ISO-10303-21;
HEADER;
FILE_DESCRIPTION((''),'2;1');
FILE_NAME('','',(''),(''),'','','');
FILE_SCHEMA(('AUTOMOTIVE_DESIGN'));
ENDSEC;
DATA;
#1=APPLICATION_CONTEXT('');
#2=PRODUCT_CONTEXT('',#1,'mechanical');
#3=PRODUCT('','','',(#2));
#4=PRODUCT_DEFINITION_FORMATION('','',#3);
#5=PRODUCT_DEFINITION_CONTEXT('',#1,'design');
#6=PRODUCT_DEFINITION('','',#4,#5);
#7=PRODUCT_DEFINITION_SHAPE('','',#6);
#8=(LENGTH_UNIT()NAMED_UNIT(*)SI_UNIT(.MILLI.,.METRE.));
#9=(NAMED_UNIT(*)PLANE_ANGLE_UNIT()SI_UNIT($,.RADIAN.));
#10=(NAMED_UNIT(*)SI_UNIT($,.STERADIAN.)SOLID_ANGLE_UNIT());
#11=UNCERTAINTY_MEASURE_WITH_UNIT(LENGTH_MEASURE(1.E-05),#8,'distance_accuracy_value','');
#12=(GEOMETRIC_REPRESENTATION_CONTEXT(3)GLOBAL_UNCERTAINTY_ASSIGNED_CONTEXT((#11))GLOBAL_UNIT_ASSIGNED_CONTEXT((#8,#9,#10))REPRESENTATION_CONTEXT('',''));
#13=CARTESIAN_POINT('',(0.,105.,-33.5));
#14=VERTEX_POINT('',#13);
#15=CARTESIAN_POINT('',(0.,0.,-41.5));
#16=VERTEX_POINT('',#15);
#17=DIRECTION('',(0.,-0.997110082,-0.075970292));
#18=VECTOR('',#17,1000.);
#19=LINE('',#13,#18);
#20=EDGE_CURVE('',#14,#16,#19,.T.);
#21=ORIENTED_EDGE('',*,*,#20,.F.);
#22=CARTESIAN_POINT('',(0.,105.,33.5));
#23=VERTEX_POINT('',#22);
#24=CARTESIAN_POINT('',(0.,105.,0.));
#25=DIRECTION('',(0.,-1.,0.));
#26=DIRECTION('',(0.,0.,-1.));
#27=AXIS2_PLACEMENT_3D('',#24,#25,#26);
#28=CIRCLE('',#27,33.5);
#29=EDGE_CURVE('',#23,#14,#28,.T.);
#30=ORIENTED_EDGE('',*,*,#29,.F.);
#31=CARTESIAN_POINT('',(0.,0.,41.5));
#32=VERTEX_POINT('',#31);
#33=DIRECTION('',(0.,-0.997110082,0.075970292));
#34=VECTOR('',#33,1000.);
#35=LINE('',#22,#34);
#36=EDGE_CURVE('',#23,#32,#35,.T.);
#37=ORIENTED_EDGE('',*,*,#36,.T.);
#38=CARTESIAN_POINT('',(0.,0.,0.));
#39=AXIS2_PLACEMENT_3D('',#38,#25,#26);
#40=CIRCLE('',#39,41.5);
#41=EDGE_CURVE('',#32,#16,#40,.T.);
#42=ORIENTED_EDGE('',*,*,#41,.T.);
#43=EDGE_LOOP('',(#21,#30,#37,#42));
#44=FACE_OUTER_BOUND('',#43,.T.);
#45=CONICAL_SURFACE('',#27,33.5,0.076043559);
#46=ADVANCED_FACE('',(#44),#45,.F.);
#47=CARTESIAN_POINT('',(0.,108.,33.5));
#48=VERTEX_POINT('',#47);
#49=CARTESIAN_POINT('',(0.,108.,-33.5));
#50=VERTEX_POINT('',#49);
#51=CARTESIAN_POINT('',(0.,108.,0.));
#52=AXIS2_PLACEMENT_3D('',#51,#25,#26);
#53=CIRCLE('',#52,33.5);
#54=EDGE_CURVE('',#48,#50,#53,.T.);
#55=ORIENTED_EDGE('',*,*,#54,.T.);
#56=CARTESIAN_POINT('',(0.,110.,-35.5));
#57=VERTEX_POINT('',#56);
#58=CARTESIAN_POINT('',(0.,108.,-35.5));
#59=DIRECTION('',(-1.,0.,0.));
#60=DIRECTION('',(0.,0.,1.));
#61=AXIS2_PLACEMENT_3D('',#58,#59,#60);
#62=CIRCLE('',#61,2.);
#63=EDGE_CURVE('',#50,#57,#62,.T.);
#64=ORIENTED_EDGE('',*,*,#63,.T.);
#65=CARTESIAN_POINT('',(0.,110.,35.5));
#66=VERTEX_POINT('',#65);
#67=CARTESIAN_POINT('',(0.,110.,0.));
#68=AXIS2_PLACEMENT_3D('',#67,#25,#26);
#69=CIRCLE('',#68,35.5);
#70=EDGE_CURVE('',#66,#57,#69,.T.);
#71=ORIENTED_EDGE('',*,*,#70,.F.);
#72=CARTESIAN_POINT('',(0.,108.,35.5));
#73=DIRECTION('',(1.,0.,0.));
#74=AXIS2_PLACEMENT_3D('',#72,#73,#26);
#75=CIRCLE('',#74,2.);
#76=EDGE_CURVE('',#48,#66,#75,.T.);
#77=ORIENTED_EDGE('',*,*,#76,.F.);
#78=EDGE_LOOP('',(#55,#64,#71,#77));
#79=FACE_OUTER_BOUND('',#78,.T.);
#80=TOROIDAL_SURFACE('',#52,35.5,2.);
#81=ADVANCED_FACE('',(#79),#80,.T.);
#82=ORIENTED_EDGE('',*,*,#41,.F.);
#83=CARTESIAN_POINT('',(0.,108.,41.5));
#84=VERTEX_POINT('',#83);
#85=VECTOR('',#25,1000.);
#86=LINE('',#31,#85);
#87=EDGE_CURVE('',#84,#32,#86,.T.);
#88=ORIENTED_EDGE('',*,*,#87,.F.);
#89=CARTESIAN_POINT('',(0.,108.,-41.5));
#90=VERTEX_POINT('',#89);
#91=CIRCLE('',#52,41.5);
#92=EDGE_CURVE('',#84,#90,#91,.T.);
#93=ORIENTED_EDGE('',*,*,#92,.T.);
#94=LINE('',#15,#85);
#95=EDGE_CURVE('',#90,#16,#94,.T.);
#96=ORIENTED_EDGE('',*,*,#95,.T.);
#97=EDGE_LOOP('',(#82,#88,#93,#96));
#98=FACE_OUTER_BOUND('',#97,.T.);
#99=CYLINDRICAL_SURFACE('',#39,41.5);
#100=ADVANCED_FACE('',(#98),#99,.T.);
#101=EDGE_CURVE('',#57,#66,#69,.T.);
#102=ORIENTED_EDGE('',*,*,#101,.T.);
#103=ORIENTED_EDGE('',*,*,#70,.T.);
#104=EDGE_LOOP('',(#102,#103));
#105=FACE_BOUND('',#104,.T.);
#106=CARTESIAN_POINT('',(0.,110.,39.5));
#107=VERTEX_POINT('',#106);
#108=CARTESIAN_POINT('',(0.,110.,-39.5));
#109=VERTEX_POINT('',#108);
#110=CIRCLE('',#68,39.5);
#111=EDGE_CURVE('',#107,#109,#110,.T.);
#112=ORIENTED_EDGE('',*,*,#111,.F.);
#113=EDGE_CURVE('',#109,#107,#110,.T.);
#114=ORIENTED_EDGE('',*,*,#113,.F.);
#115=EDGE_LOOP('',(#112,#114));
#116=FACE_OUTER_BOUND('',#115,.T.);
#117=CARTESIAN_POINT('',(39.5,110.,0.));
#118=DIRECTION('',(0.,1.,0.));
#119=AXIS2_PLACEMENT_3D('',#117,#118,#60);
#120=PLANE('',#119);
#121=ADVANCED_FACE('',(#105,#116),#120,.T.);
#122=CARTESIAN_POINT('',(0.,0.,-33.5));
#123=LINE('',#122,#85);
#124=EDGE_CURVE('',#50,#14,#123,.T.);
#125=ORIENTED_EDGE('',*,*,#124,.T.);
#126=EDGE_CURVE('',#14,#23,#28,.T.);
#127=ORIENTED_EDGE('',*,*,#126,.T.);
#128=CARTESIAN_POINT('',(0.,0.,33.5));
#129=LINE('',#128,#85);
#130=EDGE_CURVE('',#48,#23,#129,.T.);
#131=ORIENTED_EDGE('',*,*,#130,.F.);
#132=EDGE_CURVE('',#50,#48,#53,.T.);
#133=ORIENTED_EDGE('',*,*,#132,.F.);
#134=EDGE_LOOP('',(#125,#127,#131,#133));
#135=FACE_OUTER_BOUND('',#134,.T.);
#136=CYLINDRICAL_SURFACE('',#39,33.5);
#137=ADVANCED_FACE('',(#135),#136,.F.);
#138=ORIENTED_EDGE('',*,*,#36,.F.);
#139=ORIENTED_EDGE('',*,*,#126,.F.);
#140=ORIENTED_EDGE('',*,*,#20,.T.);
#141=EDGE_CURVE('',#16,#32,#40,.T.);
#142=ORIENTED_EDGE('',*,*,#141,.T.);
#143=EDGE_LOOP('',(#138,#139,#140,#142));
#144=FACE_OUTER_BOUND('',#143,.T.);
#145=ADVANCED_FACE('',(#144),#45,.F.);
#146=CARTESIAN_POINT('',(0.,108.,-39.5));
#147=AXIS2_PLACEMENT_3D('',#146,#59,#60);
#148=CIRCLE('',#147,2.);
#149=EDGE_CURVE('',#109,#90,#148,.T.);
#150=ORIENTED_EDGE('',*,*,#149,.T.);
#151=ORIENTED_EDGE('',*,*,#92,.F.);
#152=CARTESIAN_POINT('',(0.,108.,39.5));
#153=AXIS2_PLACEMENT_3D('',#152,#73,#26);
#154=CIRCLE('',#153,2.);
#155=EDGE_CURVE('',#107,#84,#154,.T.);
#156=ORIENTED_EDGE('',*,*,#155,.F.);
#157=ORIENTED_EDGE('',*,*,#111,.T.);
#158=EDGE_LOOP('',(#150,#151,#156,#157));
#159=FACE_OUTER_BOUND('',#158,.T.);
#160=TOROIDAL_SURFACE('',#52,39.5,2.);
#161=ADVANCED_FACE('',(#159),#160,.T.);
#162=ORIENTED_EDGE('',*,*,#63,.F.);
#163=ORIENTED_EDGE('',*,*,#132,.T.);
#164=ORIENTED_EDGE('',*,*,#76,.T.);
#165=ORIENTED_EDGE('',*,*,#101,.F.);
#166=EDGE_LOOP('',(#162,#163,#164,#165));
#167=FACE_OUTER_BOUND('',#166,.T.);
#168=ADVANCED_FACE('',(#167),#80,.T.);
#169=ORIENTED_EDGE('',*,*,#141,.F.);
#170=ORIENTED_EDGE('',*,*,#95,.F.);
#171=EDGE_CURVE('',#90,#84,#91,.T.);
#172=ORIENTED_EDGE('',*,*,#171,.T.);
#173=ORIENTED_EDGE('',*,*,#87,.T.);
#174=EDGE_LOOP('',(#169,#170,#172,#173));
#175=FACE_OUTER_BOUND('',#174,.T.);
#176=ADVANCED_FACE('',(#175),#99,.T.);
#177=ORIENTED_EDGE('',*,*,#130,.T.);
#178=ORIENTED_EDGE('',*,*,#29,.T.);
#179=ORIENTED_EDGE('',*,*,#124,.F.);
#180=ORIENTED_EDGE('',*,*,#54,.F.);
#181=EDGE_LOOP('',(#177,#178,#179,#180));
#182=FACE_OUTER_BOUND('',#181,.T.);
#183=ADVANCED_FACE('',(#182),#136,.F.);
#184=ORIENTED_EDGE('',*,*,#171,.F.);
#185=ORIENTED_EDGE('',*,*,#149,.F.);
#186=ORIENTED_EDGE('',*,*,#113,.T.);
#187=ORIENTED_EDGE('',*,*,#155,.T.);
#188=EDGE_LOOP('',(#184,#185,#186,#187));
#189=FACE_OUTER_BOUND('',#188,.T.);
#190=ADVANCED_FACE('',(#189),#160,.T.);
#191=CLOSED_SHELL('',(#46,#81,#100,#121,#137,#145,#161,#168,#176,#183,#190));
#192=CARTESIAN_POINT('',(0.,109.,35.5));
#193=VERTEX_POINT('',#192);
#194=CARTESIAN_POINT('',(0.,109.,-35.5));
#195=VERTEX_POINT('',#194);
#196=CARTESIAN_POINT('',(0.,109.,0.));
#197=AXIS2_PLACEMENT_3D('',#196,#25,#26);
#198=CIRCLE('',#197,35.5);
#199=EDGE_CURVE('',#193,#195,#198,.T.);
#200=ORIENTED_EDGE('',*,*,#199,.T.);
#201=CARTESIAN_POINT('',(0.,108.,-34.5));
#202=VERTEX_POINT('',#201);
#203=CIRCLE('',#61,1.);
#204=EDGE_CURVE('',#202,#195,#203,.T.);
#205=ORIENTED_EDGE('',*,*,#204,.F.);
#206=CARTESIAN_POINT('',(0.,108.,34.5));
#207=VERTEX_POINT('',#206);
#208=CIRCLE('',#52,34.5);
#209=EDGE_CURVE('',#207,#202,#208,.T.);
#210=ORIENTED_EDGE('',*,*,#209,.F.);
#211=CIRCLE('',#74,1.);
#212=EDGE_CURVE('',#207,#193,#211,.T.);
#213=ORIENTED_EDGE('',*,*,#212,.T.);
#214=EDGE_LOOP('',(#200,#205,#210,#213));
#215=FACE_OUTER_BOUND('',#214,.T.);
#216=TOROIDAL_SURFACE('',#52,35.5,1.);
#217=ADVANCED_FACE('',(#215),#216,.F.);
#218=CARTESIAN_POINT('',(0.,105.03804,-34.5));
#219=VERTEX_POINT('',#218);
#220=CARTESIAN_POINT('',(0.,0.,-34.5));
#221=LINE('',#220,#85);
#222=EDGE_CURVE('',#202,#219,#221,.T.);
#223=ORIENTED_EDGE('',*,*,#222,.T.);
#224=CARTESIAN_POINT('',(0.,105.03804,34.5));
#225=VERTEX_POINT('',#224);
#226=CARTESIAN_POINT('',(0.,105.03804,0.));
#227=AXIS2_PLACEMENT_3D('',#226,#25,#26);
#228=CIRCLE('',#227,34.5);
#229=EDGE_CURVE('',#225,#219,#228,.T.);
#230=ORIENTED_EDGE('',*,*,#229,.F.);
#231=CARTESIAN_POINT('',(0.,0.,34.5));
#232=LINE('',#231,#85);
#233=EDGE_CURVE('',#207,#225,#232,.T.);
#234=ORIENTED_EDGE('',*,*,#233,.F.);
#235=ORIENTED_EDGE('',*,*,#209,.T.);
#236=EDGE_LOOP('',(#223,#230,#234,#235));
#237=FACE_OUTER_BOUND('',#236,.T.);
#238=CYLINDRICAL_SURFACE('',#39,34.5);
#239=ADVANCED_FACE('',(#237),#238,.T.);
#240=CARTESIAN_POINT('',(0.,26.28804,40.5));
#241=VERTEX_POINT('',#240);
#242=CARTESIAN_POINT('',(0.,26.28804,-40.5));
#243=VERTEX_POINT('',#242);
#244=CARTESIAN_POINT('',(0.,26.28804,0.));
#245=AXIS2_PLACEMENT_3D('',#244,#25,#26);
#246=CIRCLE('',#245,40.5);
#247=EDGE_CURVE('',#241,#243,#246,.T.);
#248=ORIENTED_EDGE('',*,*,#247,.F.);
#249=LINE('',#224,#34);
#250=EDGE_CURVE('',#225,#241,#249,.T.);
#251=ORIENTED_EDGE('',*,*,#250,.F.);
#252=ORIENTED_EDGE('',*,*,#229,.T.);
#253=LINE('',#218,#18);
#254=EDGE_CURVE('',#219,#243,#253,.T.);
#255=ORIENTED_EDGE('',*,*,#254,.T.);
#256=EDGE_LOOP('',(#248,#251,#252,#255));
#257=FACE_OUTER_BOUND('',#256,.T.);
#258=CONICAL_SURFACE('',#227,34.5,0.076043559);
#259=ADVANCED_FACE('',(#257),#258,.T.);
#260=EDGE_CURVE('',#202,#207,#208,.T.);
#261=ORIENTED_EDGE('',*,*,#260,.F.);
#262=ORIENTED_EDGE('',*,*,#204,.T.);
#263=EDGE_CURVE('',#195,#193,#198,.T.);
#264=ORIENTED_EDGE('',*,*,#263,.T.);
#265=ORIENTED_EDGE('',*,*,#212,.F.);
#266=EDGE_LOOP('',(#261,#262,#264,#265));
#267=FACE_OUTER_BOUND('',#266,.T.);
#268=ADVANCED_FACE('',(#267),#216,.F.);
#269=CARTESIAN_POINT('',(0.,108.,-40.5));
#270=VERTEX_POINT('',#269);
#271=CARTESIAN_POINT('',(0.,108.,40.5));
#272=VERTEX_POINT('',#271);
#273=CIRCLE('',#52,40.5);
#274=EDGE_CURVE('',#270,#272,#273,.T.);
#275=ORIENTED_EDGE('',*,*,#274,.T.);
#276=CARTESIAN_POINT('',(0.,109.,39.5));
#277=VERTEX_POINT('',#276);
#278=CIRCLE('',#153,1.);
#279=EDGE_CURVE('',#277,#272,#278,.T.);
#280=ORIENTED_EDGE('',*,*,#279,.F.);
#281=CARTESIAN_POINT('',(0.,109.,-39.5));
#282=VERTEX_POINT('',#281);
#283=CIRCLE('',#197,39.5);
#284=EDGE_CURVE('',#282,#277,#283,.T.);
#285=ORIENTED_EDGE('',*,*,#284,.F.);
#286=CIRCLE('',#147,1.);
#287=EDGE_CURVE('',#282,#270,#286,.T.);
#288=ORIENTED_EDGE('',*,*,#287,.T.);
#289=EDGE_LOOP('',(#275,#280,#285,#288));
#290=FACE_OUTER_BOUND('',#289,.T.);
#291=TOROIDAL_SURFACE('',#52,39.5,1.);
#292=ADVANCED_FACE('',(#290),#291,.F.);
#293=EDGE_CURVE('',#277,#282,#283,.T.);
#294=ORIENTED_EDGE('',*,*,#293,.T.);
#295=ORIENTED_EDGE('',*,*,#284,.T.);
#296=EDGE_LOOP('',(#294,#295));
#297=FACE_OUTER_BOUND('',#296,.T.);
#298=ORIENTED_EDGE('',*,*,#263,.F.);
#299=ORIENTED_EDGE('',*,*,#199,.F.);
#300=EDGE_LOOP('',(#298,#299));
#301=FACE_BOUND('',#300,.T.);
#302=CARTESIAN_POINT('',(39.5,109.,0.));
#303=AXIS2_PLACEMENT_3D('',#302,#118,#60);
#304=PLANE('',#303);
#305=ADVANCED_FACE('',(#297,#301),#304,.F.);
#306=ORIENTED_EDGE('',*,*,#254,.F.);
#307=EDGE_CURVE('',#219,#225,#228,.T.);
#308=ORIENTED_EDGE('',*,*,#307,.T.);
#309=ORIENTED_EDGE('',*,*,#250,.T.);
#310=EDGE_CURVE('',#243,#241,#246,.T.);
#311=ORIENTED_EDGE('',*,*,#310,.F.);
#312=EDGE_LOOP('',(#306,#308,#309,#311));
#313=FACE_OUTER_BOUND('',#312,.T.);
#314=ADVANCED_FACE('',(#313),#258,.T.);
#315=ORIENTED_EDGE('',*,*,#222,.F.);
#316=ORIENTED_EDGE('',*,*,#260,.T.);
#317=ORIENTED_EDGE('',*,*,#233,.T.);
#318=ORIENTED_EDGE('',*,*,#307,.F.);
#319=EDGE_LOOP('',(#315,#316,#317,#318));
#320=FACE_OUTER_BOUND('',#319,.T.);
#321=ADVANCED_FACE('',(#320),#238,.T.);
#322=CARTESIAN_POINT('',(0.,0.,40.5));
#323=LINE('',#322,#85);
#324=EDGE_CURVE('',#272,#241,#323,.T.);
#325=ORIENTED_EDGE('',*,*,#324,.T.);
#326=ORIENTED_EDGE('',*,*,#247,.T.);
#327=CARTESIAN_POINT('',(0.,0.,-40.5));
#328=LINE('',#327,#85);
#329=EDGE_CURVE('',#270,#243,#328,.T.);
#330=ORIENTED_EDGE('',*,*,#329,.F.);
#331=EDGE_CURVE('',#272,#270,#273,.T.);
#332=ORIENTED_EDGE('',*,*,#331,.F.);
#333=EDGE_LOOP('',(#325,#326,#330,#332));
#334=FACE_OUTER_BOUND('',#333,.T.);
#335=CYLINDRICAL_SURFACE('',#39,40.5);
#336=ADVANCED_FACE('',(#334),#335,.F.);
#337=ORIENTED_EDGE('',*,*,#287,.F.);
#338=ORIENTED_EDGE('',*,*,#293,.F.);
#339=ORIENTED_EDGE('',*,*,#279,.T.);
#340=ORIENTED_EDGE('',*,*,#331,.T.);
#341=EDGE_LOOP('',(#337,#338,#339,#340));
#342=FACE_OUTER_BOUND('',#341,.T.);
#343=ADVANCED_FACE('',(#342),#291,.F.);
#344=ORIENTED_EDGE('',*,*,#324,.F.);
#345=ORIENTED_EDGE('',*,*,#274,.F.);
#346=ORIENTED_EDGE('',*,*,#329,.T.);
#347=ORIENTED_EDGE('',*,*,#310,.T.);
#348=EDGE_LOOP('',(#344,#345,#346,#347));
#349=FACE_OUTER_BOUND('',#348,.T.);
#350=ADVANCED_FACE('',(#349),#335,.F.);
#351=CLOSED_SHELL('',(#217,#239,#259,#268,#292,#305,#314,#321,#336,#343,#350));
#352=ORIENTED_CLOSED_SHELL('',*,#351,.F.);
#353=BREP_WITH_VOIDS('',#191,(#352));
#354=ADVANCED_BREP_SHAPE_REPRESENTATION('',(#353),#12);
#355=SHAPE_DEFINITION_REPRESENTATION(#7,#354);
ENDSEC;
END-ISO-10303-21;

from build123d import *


with BuildPart() as part:
    # Sketch1 → Revolve-Thin1 (revolve)
    with BuildSketch(Plane.XY, mode=Mode.PRIVATE) as revolve_thin1_sk:
        with BuildLine():
            Line((39.5, 110), (35.5, 110))
            ThreePointArc((35.5, 110), (34.085786438, 109.414213562), (33.5, 108))
            Line((33.5, 108), (33.5, 105))
            Line((33.5, 105), (41.5, 0))
            Line((41.5, 0), (41.5, 108))
            ThreePointArc((41.5, 108), (40.914213562, 109.414213562), (39.5, 110))
        make_face()
        with BuildLine():
            Line((39.5, 109), (35.5, 109))
            ThreePointArc((35.5, 109), (34.792893219, 108.707106781), (34.5, 108))
            Line((34.5, 108), (34.5, 105.038040112))
            Line((34.5, 105.038040112), (40.5, 26.288040112))
            Line((40.5, 26.288040112), (40.5, 108))
            ThreePointArc((40.5, 108), (40.207106781, 108.707106781), (39.5, 109))
        make_face(mode=Mode.SUBTRACT)
    revolve(revolve_thin1_sk.sketch.rotate(Axis((0, 0, 0), (0, 1, 0)), 90), axis=Axis((0, 0, 0), (0, 1, 0)))


solid = part.part
